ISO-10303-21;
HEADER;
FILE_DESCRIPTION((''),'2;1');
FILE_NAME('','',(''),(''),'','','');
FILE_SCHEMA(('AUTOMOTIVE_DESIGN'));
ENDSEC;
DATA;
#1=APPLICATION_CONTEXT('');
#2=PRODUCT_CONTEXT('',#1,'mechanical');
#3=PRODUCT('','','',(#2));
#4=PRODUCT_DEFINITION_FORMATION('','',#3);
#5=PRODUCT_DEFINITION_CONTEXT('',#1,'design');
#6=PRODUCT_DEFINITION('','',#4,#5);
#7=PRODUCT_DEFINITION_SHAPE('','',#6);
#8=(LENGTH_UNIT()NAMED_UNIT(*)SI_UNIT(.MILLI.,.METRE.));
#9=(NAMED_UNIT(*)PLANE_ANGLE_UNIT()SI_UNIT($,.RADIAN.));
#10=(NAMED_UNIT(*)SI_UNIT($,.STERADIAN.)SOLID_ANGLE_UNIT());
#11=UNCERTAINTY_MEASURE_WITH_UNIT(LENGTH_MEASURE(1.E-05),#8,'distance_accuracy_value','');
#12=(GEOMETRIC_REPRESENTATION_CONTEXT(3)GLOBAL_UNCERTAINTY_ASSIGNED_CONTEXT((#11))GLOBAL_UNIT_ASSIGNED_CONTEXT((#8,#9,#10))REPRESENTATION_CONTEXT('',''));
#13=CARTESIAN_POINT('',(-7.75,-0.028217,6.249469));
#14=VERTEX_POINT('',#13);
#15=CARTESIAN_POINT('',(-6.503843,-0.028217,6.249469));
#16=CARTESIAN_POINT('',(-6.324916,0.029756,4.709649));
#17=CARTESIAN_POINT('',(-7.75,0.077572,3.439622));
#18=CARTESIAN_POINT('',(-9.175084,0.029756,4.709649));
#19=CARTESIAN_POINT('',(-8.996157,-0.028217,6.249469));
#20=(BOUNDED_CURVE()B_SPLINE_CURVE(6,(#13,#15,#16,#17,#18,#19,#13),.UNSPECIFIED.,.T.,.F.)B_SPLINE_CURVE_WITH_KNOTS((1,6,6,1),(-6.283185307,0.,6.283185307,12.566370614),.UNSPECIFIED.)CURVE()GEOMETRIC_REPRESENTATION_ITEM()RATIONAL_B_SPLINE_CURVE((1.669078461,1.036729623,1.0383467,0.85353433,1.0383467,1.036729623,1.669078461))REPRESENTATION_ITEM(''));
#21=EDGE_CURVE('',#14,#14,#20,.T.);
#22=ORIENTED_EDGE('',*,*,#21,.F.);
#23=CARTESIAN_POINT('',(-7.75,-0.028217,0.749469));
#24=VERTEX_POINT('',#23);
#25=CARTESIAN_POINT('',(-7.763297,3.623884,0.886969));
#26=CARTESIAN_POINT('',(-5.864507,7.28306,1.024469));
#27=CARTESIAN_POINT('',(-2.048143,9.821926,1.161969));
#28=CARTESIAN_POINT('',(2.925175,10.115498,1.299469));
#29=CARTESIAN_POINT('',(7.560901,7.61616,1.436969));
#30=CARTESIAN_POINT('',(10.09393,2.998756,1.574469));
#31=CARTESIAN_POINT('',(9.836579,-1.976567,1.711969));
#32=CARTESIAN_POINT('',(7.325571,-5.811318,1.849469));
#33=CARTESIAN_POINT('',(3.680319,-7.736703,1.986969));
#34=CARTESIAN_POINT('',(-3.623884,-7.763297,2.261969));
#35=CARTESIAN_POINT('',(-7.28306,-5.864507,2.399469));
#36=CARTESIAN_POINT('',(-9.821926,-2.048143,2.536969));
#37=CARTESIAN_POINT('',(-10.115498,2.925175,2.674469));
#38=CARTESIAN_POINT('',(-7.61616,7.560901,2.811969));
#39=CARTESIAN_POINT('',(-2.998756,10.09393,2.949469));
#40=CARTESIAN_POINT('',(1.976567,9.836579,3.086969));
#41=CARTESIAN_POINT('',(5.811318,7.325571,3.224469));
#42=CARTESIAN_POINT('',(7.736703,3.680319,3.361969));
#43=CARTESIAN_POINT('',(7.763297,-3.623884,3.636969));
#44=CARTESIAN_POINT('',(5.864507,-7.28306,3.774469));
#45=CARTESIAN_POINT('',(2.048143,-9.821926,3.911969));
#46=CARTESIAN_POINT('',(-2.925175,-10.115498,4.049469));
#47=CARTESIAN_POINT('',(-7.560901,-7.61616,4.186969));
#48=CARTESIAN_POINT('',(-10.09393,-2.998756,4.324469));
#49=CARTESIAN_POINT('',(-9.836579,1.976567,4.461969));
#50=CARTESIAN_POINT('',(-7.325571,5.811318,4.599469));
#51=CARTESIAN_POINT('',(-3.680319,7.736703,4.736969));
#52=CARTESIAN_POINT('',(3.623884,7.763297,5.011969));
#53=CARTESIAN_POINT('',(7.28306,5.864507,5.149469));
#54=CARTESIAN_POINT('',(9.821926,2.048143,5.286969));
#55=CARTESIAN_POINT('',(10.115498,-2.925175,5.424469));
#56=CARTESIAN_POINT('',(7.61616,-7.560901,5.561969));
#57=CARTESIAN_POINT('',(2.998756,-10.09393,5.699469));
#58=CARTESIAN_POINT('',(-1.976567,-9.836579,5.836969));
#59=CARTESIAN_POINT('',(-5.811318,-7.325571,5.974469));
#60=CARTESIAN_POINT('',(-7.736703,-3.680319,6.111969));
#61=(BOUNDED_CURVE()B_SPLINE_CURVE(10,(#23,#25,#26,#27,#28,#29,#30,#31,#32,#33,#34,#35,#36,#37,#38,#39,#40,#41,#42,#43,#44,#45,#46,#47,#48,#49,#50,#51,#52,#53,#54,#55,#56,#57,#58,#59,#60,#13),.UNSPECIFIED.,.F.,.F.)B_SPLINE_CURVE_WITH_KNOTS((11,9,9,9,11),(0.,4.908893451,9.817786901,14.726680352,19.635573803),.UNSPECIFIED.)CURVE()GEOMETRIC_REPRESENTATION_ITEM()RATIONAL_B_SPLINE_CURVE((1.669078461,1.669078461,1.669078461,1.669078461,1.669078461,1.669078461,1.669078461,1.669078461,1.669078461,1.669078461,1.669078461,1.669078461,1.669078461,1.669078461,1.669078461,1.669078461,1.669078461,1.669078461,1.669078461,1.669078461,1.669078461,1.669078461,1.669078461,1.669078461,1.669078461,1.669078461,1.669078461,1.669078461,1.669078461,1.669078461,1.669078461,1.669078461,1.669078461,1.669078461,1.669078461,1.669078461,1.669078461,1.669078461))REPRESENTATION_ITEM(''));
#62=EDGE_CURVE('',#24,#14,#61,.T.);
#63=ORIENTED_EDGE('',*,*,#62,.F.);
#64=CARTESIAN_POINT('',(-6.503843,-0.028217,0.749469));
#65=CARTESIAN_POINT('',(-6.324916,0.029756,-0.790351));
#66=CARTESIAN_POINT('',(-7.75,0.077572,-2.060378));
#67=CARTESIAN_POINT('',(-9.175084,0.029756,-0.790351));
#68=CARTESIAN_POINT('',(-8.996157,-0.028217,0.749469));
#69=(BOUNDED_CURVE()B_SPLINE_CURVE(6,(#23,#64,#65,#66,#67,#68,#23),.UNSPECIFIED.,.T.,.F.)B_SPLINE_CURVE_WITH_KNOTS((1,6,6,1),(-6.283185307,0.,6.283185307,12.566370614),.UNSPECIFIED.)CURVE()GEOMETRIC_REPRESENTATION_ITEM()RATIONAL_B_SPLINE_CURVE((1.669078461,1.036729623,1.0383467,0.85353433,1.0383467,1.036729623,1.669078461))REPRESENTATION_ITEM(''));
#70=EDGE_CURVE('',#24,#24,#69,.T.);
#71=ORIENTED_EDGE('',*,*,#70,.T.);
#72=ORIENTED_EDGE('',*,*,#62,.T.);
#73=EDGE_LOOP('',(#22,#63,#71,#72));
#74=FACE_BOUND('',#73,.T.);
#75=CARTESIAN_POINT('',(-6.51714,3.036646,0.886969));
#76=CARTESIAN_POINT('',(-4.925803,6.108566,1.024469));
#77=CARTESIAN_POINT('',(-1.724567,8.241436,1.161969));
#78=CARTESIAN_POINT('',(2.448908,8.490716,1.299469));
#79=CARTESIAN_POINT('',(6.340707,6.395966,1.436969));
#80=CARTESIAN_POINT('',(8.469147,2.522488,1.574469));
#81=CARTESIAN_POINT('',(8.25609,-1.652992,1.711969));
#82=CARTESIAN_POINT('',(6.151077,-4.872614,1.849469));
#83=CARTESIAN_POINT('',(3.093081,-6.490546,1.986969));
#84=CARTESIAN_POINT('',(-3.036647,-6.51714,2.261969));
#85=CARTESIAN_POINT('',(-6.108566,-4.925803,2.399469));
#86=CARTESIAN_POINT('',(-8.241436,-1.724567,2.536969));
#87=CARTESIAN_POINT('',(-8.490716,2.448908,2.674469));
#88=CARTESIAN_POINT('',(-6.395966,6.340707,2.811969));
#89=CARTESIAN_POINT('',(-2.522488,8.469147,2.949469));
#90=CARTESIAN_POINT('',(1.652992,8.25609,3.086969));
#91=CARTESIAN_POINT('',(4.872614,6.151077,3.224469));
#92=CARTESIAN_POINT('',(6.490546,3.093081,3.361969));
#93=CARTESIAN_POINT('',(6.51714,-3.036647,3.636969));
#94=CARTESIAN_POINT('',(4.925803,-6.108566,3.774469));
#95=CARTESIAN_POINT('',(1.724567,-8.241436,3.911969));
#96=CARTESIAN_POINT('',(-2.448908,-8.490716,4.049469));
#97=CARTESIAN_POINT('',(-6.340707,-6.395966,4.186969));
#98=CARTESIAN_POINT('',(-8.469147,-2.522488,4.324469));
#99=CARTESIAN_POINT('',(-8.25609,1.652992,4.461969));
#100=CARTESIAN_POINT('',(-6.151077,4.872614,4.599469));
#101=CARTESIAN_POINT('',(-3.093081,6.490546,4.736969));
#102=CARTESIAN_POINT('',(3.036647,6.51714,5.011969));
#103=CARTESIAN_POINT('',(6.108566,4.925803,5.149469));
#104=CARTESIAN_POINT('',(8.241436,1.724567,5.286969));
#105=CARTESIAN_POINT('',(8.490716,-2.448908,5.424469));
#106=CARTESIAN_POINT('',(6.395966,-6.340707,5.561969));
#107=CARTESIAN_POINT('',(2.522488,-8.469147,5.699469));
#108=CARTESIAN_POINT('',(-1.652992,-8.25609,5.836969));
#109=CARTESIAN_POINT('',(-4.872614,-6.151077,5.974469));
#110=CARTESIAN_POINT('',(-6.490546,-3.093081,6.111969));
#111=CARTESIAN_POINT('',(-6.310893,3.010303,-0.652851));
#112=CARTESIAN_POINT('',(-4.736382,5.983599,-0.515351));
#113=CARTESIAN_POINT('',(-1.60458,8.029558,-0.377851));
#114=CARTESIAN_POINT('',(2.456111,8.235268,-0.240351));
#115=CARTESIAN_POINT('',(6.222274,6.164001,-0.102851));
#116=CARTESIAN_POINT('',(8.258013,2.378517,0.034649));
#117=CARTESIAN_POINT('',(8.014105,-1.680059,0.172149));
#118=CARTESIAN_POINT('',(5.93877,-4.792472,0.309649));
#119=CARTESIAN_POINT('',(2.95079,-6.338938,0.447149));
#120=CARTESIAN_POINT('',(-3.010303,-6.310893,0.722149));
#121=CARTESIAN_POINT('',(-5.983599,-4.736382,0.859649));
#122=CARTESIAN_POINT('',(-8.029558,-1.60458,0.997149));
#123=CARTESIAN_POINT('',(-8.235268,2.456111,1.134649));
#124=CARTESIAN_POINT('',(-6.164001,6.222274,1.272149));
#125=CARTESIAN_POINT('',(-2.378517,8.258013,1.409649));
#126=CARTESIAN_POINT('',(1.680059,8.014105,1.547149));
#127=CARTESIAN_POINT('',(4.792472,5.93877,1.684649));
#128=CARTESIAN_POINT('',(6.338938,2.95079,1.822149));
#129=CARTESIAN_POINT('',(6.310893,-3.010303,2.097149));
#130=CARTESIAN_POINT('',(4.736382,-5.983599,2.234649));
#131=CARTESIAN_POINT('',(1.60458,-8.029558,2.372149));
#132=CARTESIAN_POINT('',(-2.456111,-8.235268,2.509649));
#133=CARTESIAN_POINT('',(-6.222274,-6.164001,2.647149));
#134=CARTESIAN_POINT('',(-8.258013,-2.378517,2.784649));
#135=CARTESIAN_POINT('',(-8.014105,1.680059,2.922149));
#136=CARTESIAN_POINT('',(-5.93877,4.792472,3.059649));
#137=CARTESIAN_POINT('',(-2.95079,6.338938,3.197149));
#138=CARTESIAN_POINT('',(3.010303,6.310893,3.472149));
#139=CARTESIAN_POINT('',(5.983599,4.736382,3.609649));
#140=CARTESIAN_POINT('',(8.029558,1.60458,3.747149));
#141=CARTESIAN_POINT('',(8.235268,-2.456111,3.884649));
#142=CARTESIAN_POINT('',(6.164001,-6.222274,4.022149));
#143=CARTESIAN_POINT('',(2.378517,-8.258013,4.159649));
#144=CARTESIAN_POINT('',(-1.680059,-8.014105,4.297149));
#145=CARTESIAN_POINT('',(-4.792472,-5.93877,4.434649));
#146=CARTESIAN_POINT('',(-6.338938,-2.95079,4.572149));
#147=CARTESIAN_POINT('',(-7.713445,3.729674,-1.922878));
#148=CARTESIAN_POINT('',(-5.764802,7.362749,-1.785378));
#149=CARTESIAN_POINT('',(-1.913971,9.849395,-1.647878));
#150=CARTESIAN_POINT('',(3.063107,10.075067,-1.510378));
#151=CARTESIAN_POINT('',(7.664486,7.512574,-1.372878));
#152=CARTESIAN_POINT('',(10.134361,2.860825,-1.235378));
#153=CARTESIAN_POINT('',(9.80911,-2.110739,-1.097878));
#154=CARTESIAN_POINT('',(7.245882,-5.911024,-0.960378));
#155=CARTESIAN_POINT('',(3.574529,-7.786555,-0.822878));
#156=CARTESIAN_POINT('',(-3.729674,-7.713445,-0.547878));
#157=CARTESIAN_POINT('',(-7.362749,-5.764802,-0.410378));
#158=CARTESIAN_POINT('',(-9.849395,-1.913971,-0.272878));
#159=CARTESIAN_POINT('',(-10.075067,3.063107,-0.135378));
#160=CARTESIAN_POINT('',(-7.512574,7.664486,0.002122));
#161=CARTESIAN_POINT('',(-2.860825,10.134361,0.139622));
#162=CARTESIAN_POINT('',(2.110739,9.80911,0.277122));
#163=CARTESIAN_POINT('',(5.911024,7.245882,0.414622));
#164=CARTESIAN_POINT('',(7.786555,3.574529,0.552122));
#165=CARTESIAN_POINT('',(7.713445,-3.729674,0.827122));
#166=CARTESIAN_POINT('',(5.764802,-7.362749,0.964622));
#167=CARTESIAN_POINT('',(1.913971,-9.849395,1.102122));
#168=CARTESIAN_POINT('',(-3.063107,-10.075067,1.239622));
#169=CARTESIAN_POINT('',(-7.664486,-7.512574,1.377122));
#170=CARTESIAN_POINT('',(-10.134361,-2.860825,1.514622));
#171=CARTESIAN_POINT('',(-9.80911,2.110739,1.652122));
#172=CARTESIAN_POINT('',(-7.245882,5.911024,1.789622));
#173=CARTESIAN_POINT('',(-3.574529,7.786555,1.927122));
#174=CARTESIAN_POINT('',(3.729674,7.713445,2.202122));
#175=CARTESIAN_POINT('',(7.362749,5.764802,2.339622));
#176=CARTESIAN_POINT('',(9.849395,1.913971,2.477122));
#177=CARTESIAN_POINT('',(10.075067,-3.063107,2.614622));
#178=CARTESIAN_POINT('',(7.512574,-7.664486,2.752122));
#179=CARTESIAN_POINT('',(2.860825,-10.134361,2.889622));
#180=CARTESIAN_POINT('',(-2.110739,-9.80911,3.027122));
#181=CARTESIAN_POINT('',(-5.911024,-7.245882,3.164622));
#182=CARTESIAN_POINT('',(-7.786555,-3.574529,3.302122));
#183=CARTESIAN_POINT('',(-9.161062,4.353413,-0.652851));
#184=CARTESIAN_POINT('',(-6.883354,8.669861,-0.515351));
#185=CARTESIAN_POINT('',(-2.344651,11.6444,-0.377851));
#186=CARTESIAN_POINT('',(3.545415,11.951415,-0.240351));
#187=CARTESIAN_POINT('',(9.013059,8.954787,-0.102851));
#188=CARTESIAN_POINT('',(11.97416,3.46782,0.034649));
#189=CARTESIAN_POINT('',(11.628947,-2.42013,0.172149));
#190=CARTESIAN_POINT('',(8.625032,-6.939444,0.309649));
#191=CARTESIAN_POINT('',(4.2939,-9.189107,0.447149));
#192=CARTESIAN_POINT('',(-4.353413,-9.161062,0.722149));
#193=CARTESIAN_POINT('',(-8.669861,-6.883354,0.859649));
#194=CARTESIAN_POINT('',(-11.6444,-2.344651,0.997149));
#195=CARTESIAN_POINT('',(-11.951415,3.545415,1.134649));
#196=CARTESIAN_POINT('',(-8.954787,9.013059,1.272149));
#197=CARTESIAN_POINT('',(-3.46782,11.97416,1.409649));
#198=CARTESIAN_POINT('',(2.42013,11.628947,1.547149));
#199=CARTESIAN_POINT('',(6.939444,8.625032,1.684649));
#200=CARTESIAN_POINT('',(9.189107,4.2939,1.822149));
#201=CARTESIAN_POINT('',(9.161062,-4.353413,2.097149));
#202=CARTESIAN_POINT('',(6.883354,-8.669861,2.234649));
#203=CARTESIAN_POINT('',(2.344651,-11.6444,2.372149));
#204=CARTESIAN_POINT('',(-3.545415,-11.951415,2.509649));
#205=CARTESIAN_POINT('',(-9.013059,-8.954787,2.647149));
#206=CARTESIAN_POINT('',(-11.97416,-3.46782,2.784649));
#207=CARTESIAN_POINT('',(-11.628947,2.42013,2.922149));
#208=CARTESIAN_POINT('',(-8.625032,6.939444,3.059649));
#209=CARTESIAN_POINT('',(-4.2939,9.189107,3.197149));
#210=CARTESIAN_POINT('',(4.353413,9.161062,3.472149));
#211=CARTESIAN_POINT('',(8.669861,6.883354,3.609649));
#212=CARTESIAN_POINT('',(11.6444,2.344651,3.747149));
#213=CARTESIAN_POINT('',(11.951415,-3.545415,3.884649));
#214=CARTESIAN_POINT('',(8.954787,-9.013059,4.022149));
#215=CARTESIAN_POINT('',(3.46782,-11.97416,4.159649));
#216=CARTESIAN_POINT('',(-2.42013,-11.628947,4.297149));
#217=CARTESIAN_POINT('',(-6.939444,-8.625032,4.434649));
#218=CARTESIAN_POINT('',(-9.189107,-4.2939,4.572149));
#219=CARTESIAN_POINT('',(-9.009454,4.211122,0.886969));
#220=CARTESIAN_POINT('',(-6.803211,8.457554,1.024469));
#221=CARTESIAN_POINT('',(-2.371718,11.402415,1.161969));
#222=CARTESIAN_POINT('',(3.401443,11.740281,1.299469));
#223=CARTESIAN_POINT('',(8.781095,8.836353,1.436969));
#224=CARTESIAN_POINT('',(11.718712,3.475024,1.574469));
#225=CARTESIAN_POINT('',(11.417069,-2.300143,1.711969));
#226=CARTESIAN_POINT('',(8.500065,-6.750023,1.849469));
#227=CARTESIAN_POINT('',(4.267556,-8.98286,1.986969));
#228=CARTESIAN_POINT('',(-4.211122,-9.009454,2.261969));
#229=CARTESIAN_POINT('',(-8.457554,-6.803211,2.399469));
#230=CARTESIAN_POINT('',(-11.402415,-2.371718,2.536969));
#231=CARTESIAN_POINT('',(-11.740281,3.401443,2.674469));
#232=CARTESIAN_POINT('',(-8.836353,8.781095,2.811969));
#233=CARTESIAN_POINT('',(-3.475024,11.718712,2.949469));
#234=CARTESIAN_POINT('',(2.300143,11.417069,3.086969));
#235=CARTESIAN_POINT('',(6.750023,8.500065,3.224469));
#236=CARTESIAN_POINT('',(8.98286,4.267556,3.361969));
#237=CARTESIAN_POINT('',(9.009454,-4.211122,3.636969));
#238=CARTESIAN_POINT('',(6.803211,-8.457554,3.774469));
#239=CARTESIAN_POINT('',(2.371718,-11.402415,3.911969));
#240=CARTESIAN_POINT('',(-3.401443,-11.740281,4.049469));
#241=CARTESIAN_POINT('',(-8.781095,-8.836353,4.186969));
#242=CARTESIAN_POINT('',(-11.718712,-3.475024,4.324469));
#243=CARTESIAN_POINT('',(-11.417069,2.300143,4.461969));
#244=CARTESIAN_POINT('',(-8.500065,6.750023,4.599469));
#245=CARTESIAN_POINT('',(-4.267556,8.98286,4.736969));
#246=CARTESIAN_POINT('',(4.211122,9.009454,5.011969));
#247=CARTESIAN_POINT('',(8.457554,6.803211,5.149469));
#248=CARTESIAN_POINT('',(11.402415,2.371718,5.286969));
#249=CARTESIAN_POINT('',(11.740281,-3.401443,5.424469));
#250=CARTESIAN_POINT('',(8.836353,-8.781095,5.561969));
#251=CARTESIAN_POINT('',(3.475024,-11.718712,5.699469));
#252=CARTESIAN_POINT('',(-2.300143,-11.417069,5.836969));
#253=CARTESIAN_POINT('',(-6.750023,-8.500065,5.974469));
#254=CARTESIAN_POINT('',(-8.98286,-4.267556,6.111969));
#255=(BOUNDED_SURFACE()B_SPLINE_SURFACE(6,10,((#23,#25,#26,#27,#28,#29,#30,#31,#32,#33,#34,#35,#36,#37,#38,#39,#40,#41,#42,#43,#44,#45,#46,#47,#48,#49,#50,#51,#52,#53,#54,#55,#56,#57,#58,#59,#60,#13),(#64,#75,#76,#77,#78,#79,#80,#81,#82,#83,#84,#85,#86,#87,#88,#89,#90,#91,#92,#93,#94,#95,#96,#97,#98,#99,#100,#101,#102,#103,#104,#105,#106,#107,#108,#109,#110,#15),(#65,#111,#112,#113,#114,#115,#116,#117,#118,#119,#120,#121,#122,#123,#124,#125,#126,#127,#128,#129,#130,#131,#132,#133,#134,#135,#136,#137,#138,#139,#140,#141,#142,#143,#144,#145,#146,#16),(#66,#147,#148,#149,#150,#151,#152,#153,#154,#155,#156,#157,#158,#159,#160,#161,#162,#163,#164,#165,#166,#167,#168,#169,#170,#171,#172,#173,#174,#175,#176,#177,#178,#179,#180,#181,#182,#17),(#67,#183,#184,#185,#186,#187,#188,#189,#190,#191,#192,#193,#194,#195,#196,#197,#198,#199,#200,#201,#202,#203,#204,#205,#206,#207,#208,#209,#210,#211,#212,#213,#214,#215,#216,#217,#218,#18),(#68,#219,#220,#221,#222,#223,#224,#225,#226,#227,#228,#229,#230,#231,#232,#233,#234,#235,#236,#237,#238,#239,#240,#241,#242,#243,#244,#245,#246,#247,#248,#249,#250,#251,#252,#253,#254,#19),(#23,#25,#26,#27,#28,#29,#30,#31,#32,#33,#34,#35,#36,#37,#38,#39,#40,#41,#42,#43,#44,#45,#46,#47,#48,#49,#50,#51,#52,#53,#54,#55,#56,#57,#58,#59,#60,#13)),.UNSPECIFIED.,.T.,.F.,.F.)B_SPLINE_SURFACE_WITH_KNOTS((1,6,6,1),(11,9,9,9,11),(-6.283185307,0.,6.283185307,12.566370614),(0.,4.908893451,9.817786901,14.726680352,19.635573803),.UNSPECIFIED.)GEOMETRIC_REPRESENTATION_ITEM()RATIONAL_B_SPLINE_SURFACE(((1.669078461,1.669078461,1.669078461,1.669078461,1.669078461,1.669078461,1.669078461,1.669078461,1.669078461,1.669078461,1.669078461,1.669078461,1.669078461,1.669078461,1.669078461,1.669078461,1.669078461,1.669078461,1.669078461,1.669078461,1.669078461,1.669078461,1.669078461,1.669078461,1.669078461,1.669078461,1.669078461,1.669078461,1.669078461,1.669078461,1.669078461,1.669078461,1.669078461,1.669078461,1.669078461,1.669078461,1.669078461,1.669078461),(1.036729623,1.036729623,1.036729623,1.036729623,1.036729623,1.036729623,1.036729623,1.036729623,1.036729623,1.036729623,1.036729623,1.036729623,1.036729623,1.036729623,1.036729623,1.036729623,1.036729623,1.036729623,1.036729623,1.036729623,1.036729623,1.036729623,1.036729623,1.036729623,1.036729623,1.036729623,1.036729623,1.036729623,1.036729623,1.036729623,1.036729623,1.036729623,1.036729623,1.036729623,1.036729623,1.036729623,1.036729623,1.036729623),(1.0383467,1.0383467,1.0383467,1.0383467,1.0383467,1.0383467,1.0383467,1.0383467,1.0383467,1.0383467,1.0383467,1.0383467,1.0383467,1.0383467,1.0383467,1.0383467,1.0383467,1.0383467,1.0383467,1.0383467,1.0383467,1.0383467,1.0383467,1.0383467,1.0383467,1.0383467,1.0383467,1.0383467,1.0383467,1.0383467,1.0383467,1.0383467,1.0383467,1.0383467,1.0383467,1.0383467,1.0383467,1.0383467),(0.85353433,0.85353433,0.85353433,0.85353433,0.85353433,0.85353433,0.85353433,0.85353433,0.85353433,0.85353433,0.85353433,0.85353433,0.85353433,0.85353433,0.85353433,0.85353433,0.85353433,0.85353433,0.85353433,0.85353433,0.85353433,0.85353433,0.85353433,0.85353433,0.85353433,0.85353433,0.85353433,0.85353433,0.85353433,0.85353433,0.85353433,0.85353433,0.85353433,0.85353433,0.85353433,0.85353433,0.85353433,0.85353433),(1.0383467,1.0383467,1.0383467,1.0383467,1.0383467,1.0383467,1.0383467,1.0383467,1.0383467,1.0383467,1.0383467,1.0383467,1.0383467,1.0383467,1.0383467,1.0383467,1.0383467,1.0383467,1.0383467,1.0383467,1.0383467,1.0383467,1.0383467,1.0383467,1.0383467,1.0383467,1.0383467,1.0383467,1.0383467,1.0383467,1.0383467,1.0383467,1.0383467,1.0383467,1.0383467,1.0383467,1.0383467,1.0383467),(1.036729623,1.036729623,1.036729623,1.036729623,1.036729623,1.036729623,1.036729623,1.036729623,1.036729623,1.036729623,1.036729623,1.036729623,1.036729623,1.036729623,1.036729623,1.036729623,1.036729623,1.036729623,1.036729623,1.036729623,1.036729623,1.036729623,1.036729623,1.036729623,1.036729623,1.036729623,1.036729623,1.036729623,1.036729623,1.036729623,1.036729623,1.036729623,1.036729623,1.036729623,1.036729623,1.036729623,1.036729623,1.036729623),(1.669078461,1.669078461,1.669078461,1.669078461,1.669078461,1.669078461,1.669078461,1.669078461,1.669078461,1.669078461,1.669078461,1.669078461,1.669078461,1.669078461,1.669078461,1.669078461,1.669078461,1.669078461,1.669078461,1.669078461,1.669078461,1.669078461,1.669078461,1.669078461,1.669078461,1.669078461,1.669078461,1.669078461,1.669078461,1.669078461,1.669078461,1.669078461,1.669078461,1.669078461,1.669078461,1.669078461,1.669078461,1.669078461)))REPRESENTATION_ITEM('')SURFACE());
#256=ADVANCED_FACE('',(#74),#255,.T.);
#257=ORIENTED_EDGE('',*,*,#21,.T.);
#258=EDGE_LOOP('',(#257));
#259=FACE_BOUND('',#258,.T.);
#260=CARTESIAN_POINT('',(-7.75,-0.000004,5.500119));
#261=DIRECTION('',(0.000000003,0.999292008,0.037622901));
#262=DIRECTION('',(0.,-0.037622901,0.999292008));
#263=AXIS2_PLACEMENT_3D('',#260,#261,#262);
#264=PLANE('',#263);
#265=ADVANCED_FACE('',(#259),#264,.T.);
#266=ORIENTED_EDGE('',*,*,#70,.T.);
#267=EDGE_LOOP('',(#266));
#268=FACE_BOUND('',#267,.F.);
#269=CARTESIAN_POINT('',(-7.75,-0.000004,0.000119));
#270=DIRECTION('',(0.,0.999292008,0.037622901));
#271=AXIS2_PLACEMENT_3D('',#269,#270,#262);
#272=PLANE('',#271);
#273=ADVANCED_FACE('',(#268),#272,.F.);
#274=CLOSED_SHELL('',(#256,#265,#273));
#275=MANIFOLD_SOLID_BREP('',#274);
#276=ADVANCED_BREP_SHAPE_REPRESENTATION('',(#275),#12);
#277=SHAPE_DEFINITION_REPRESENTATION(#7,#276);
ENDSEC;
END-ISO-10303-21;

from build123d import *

# Parameters (mm, degrees)
SWEEP1_PITCH       = 1.833333333
SWEEP1_HEIGHT      = 5.5
SWEEP1_RADIUS      = 7.75
SWEEP1_START_ANGLE = -180
SWEEP1_PROFILE_R   = 0.75


with BuildPart() as part:
    # Sweep1: sweep along a helix
    with BuildLine() as sweep1_path:
        add(Helix(SWEEP1_PITCH, SWEEP1_HEIGHT, SWEEP1_RADIUS, center=(0, 0, 0), direction=(0, 0, 1), lefthand=True, mode=Mode.PRIVATE).rotate(Axis((0, 0, 0), (0, 0, 1)), SWEEP1_START_ANGLE))
    # Sweep1 profile (on start of the path) → Sweep1 (sweep)
    with BuildSketch(Plane(origin=(-7.75, 0, 0), x_dir=(0, -0.03762290084709483, 0.9992920080396169), z_dir=(-1.5637846105898416e-13, 0.9992920080396169, 0.03762290084709483))):
        Circle(SWEEP1_PROFILE_R)
    sweep(path=sweep1_path.line, is_frenet=True)


solid = part.part
